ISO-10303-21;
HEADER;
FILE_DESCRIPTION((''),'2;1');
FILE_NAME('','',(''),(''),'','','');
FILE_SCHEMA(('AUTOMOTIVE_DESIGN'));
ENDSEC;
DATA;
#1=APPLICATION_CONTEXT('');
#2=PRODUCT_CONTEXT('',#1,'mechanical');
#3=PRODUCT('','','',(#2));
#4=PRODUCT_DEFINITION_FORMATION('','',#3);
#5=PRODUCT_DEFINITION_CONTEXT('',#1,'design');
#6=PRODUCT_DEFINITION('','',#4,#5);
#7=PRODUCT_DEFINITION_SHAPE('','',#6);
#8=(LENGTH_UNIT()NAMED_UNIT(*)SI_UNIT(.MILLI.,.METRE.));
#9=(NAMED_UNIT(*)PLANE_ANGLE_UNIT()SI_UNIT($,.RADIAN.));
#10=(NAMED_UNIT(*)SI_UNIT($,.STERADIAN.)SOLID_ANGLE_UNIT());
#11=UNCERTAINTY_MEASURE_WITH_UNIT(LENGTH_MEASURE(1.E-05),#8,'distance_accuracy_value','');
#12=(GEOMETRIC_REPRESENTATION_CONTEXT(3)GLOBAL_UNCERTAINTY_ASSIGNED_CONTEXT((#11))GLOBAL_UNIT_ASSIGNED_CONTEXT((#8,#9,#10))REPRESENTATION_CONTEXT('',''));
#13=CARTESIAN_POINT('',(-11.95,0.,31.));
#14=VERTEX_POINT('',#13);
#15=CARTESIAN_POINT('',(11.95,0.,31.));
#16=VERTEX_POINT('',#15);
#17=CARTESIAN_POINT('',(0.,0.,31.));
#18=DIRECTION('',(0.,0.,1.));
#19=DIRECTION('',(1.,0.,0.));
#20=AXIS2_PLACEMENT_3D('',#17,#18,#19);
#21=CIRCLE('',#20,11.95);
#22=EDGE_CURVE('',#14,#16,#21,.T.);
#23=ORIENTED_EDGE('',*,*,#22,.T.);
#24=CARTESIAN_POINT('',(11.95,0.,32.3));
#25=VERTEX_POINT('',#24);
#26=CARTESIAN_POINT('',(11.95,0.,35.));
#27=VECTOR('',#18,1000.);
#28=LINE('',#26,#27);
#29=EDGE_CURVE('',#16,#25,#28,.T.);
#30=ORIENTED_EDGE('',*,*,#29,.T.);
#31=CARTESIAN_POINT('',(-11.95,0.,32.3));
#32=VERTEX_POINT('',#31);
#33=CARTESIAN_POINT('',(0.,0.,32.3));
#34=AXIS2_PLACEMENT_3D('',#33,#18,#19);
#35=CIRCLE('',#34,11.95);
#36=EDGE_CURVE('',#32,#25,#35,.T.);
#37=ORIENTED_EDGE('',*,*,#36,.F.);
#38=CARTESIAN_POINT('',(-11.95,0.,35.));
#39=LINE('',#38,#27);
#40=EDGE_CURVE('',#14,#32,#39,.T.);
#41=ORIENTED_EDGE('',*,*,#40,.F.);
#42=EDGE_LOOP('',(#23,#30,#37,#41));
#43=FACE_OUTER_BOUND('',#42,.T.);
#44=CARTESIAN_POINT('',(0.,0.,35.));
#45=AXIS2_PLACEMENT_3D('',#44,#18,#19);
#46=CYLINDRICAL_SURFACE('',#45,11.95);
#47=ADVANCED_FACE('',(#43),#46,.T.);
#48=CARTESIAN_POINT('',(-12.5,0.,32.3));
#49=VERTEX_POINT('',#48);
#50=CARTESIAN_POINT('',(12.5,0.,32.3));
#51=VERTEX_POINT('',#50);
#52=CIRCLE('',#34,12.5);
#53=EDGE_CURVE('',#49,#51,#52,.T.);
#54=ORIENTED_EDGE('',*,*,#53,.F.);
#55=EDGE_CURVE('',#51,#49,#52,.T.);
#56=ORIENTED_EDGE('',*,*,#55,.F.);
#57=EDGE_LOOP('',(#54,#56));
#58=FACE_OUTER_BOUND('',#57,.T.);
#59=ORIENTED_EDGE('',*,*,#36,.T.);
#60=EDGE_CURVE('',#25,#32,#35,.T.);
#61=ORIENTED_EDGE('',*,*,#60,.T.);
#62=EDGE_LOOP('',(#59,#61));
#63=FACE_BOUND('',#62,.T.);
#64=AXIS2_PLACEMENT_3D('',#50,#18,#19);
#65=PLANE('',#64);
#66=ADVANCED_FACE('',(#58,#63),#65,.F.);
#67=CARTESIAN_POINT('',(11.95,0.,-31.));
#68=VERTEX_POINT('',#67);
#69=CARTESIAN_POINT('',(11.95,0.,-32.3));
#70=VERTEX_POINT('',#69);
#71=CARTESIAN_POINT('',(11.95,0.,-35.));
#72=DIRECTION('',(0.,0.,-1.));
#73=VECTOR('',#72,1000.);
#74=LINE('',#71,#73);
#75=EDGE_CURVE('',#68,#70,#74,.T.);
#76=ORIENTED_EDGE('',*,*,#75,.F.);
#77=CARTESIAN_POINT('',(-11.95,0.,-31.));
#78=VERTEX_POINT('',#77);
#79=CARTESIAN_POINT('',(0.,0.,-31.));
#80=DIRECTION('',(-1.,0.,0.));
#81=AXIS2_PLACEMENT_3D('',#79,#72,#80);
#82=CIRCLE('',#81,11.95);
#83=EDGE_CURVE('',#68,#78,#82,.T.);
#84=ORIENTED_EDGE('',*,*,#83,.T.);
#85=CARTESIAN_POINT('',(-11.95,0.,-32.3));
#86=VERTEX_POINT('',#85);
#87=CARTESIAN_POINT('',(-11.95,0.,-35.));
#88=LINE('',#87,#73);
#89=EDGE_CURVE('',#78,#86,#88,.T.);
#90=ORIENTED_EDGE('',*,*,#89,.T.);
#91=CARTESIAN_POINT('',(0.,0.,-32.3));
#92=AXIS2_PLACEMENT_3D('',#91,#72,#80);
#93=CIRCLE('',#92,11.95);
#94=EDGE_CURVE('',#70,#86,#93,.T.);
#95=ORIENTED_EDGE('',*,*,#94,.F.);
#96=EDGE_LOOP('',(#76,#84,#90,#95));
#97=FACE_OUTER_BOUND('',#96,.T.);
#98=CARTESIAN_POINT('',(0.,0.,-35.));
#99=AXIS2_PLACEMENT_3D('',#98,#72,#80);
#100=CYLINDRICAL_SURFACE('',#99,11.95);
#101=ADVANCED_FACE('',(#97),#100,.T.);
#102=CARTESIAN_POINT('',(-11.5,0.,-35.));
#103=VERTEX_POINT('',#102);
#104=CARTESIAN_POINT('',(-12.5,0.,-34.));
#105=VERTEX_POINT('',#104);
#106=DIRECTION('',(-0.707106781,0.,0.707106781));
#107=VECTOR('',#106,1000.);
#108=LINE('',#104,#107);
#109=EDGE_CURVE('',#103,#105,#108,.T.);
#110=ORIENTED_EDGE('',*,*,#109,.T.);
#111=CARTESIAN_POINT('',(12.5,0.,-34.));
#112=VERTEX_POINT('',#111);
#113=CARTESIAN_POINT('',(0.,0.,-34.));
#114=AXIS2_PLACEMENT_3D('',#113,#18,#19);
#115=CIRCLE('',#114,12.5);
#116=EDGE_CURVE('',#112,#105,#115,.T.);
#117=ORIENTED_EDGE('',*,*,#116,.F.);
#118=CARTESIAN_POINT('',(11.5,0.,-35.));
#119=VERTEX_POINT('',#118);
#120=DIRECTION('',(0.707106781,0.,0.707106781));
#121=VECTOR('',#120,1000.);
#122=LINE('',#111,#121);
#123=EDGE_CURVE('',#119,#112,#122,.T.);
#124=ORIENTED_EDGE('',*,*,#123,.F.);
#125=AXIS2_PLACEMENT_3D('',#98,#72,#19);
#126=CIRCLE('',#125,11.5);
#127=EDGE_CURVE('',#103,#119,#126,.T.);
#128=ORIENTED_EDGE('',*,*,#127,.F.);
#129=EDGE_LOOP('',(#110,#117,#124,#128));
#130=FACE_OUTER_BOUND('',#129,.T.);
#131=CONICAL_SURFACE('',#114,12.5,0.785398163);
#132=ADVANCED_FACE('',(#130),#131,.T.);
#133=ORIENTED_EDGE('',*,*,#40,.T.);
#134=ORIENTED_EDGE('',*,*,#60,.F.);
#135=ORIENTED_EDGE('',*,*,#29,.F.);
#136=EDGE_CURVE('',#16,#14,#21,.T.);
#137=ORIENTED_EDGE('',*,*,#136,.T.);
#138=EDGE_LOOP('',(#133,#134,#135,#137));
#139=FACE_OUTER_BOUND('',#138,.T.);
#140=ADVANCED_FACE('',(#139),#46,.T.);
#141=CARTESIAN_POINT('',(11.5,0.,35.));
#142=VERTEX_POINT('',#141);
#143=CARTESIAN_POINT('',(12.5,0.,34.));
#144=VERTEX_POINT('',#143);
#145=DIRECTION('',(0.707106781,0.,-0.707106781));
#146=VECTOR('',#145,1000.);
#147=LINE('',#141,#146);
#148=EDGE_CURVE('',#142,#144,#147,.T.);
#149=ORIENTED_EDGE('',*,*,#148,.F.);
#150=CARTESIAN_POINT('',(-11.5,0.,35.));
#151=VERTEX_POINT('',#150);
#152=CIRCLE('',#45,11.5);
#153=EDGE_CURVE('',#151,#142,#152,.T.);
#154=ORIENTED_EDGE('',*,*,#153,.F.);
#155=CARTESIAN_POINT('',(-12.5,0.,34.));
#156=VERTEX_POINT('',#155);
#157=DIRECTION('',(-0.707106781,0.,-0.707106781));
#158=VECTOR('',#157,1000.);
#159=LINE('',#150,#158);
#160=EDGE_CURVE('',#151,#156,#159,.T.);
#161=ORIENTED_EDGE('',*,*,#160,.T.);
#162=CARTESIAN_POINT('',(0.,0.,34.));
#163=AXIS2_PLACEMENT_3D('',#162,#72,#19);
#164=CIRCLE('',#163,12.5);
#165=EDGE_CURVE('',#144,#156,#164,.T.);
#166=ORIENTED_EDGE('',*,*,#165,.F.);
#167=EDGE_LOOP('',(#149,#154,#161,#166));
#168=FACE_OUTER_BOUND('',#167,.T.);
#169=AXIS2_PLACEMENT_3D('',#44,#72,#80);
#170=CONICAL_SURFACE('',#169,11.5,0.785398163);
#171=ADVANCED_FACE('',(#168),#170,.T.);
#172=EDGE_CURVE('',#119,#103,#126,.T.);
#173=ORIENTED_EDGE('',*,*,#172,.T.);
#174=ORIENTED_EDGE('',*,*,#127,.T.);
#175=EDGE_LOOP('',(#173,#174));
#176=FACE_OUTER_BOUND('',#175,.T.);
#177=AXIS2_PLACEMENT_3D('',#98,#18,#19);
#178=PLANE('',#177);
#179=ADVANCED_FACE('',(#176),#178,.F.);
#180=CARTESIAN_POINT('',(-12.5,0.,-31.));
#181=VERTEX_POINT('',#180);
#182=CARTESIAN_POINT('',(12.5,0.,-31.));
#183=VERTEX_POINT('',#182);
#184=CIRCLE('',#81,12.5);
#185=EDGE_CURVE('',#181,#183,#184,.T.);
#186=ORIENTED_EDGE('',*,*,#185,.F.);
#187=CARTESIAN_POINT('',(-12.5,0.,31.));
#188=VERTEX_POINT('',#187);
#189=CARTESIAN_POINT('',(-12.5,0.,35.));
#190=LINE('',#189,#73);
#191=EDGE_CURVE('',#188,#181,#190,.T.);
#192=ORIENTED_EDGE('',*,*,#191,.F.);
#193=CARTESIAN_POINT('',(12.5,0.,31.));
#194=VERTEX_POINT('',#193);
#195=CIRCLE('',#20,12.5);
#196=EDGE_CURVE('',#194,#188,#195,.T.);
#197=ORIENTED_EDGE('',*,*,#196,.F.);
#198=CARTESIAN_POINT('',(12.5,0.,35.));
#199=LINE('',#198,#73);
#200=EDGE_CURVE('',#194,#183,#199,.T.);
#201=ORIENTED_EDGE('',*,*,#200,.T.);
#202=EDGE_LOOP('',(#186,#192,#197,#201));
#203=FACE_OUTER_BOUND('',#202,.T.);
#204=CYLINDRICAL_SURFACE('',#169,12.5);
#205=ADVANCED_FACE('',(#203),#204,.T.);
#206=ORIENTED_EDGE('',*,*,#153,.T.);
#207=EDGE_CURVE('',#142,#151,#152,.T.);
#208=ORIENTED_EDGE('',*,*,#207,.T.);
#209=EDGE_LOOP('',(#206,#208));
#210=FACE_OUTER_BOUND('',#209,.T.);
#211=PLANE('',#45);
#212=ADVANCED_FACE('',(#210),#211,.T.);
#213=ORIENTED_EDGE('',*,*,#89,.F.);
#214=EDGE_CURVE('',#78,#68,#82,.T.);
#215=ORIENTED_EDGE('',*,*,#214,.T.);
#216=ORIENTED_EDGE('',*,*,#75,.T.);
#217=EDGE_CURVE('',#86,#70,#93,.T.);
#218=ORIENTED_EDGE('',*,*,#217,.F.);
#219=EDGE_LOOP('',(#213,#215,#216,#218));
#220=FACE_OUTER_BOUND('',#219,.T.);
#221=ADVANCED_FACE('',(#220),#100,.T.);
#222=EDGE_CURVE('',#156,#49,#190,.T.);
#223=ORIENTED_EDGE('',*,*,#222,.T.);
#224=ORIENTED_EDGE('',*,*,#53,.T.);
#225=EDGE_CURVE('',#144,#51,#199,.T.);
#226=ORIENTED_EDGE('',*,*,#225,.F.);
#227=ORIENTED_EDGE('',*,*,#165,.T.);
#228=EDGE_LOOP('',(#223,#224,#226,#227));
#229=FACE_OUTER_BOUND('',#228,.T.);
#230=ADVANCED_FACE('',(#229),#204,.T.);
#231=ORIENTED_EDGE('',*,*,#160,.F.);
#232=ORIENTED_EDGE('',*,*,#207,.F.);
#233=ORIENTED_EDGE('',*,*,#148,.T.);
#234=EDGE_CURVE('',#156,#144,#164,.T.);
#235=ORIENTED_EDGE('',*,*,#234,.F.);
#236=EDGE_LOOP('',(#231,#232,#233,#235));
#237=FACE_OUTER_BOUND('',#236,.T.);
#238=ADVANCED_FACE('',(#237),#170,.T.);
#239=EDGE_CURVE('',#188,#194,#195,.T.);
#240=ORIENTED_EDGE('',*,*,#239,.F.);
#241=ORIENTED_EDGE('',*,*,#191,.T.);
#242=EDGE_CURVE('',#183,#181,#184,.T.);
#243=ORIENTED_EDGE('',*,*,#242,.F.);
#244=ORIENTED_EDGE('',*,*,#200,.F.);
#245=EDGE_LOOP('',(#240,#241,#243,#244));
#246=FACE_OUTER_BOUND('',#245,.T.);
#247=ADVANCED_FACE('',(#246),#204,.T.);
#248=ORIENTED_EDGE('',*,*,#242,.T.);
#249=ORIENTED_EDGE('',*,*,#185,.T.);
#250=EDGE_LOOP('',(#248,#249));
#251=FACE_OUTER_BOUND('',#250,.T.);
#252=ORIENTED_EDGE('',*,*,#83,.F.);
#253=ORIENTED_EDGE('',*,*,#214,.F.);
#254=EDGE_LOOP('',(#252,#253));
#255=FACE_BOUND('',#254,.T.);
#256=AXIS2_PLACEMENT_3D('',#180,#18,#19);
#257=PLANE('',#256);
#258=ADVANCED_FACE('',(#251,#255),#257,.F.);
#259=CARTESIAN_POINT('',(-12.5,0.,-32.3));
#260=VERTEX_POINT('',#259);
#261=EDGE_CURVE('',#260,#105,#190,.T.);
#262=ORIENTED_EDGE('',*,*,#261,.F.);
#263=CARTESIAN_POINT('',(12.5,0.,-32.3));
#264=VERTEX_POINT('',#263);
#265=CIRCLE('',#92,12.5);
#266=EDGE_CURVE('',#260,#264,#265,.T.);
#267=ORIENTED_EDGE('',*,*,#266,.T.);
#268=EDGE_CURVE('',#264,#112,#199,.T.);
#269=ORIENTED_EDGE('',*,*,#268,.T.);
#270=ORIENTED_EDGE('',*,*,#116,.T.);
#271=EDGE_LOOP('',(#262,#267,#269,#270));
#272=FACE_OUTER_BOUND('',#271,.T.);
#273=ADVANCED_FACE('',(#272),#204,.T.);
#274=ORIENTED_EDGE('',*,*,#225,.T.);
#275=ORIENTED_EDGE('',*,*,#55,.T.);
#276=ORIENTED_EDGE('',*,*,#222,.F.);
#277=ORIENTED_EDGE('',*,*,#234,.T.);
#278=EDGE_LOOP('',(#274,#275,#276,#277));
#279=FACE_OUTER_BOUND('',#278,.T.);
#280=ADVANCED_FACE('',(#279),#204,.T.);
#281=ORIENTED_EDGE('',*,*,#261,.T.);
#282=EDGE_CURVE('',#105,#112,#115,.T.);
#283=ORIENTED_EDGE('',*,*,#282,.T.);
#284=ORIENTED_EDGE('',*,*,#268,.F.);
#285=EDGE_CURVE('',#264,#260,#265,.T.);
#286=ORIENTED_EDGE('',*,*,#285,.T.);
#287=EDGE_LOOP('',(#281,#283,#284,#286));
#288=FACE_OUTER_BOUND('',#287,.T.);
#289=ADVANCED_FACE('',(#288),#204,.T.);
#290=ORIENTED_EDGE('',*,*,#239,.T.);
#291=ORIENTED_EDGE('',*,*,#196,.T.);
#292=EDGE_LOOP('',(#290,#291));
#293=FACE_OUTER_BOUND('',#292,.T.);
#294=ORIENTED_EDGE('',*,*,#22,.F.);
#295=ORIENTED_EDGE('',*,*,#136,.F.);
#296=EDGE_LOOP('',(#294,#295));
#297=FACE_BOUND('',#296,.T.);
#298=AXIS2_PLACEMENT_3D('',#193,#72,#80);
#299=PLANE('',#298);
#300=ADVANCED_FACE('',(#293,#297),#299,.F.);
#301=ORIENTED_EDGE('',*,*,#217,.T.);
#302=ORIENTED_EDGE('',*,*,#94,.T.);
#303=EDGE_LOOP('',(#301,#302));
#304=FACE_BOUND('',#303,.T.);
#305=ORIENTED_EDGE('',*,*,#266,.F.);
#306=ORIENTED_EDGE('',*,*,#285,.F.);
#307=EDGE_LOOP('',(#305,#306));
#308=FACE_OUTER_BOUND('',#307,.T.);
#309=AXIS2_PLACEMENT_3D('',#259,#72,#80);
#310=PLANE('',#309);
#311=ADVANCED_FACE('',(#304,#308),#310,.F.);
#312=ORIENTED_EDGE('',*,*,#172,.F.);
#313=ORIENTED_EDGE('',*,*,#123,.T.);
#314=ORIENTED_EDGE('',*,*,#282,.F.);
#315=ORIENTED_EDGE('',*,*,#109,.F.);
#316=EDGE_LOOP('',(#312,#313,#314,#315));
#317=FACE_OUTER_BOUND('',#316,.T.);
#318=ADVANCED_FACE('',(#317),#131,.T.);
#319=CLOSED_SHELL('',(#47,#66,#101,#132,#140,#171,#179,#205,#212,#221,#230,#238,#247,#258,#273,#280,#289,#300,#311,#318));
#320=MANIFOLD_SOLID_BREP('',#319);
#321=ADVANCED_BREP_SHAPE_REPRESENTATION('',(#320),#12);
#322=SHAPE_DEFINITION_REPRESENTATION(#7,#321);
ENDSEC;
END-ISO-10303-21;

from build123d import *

# Parameters (mm, degrees)
SKETCH_1_R      = 12.5
EXTRUDE_1_DEPTH = 35
SKETCH_3_W      = 1.3
SKETCH_3_H      = 0.55
SKETCH_31_W     = 1.3
SKETCH_31_H     = 0.55
CHAMFER_1_SIZE  = 1


with BuildPart() as part:
    # 草图1 → 凸台-拉伸1 (new, symmetric)
    with BuildSketch(Plane.XY):
        Circle(SKETCH_1_R)
    extrude(amount=EXTRUDE_1_DEPTH, both=True)

    # 草图3 → 切除-旋转1 (revolve, cut)
    with BuildSketch(Plane(origin=(-100, 0, -35), x_dir=(0, 0, 1), z_dir=(0, 1, 0))):
        with Locations((3.35, 87.775)):
            Rectangle(SKETCH_3_W, SKETCH_3_H)
    revolve(axis=Axis((0, 0, -35), (0, 0, 1)), mode=Mode.SUBTRACT)

    # 草图31 → 切除-旋转11 (revolve, cut)
    with BuildSketch(Plane(origin=(100, 0, 35), x_dir=(0, 0, -1), z_dir=(0, 1, 0)), mode=Mode.PRIVATE) as cut_revolve_11_sk:
        with Locations((3.35, 87.775)):
            Rectangle(SKETCH_31_W, SKETCH_31_H)
    revolve(cut_revolve_11_sk.sketch.rotate(Axis((0, 0, 35), (0, 0, -1)), 180), axis=Axis((0, 0, 35), (0, 0, -1)), mode=Mode.SUBTRACT)

    # 倒角1
    chamfer_1_edges = [part.edges().sort_by_distance(p)[0] for p in [
        (-12.5, 0, -35),
        (-12.5, 0, 35),
    ]]
    chamfer(chamfer_1_edges, length=CHAMFER_1_SIZE)


solid = part.part
